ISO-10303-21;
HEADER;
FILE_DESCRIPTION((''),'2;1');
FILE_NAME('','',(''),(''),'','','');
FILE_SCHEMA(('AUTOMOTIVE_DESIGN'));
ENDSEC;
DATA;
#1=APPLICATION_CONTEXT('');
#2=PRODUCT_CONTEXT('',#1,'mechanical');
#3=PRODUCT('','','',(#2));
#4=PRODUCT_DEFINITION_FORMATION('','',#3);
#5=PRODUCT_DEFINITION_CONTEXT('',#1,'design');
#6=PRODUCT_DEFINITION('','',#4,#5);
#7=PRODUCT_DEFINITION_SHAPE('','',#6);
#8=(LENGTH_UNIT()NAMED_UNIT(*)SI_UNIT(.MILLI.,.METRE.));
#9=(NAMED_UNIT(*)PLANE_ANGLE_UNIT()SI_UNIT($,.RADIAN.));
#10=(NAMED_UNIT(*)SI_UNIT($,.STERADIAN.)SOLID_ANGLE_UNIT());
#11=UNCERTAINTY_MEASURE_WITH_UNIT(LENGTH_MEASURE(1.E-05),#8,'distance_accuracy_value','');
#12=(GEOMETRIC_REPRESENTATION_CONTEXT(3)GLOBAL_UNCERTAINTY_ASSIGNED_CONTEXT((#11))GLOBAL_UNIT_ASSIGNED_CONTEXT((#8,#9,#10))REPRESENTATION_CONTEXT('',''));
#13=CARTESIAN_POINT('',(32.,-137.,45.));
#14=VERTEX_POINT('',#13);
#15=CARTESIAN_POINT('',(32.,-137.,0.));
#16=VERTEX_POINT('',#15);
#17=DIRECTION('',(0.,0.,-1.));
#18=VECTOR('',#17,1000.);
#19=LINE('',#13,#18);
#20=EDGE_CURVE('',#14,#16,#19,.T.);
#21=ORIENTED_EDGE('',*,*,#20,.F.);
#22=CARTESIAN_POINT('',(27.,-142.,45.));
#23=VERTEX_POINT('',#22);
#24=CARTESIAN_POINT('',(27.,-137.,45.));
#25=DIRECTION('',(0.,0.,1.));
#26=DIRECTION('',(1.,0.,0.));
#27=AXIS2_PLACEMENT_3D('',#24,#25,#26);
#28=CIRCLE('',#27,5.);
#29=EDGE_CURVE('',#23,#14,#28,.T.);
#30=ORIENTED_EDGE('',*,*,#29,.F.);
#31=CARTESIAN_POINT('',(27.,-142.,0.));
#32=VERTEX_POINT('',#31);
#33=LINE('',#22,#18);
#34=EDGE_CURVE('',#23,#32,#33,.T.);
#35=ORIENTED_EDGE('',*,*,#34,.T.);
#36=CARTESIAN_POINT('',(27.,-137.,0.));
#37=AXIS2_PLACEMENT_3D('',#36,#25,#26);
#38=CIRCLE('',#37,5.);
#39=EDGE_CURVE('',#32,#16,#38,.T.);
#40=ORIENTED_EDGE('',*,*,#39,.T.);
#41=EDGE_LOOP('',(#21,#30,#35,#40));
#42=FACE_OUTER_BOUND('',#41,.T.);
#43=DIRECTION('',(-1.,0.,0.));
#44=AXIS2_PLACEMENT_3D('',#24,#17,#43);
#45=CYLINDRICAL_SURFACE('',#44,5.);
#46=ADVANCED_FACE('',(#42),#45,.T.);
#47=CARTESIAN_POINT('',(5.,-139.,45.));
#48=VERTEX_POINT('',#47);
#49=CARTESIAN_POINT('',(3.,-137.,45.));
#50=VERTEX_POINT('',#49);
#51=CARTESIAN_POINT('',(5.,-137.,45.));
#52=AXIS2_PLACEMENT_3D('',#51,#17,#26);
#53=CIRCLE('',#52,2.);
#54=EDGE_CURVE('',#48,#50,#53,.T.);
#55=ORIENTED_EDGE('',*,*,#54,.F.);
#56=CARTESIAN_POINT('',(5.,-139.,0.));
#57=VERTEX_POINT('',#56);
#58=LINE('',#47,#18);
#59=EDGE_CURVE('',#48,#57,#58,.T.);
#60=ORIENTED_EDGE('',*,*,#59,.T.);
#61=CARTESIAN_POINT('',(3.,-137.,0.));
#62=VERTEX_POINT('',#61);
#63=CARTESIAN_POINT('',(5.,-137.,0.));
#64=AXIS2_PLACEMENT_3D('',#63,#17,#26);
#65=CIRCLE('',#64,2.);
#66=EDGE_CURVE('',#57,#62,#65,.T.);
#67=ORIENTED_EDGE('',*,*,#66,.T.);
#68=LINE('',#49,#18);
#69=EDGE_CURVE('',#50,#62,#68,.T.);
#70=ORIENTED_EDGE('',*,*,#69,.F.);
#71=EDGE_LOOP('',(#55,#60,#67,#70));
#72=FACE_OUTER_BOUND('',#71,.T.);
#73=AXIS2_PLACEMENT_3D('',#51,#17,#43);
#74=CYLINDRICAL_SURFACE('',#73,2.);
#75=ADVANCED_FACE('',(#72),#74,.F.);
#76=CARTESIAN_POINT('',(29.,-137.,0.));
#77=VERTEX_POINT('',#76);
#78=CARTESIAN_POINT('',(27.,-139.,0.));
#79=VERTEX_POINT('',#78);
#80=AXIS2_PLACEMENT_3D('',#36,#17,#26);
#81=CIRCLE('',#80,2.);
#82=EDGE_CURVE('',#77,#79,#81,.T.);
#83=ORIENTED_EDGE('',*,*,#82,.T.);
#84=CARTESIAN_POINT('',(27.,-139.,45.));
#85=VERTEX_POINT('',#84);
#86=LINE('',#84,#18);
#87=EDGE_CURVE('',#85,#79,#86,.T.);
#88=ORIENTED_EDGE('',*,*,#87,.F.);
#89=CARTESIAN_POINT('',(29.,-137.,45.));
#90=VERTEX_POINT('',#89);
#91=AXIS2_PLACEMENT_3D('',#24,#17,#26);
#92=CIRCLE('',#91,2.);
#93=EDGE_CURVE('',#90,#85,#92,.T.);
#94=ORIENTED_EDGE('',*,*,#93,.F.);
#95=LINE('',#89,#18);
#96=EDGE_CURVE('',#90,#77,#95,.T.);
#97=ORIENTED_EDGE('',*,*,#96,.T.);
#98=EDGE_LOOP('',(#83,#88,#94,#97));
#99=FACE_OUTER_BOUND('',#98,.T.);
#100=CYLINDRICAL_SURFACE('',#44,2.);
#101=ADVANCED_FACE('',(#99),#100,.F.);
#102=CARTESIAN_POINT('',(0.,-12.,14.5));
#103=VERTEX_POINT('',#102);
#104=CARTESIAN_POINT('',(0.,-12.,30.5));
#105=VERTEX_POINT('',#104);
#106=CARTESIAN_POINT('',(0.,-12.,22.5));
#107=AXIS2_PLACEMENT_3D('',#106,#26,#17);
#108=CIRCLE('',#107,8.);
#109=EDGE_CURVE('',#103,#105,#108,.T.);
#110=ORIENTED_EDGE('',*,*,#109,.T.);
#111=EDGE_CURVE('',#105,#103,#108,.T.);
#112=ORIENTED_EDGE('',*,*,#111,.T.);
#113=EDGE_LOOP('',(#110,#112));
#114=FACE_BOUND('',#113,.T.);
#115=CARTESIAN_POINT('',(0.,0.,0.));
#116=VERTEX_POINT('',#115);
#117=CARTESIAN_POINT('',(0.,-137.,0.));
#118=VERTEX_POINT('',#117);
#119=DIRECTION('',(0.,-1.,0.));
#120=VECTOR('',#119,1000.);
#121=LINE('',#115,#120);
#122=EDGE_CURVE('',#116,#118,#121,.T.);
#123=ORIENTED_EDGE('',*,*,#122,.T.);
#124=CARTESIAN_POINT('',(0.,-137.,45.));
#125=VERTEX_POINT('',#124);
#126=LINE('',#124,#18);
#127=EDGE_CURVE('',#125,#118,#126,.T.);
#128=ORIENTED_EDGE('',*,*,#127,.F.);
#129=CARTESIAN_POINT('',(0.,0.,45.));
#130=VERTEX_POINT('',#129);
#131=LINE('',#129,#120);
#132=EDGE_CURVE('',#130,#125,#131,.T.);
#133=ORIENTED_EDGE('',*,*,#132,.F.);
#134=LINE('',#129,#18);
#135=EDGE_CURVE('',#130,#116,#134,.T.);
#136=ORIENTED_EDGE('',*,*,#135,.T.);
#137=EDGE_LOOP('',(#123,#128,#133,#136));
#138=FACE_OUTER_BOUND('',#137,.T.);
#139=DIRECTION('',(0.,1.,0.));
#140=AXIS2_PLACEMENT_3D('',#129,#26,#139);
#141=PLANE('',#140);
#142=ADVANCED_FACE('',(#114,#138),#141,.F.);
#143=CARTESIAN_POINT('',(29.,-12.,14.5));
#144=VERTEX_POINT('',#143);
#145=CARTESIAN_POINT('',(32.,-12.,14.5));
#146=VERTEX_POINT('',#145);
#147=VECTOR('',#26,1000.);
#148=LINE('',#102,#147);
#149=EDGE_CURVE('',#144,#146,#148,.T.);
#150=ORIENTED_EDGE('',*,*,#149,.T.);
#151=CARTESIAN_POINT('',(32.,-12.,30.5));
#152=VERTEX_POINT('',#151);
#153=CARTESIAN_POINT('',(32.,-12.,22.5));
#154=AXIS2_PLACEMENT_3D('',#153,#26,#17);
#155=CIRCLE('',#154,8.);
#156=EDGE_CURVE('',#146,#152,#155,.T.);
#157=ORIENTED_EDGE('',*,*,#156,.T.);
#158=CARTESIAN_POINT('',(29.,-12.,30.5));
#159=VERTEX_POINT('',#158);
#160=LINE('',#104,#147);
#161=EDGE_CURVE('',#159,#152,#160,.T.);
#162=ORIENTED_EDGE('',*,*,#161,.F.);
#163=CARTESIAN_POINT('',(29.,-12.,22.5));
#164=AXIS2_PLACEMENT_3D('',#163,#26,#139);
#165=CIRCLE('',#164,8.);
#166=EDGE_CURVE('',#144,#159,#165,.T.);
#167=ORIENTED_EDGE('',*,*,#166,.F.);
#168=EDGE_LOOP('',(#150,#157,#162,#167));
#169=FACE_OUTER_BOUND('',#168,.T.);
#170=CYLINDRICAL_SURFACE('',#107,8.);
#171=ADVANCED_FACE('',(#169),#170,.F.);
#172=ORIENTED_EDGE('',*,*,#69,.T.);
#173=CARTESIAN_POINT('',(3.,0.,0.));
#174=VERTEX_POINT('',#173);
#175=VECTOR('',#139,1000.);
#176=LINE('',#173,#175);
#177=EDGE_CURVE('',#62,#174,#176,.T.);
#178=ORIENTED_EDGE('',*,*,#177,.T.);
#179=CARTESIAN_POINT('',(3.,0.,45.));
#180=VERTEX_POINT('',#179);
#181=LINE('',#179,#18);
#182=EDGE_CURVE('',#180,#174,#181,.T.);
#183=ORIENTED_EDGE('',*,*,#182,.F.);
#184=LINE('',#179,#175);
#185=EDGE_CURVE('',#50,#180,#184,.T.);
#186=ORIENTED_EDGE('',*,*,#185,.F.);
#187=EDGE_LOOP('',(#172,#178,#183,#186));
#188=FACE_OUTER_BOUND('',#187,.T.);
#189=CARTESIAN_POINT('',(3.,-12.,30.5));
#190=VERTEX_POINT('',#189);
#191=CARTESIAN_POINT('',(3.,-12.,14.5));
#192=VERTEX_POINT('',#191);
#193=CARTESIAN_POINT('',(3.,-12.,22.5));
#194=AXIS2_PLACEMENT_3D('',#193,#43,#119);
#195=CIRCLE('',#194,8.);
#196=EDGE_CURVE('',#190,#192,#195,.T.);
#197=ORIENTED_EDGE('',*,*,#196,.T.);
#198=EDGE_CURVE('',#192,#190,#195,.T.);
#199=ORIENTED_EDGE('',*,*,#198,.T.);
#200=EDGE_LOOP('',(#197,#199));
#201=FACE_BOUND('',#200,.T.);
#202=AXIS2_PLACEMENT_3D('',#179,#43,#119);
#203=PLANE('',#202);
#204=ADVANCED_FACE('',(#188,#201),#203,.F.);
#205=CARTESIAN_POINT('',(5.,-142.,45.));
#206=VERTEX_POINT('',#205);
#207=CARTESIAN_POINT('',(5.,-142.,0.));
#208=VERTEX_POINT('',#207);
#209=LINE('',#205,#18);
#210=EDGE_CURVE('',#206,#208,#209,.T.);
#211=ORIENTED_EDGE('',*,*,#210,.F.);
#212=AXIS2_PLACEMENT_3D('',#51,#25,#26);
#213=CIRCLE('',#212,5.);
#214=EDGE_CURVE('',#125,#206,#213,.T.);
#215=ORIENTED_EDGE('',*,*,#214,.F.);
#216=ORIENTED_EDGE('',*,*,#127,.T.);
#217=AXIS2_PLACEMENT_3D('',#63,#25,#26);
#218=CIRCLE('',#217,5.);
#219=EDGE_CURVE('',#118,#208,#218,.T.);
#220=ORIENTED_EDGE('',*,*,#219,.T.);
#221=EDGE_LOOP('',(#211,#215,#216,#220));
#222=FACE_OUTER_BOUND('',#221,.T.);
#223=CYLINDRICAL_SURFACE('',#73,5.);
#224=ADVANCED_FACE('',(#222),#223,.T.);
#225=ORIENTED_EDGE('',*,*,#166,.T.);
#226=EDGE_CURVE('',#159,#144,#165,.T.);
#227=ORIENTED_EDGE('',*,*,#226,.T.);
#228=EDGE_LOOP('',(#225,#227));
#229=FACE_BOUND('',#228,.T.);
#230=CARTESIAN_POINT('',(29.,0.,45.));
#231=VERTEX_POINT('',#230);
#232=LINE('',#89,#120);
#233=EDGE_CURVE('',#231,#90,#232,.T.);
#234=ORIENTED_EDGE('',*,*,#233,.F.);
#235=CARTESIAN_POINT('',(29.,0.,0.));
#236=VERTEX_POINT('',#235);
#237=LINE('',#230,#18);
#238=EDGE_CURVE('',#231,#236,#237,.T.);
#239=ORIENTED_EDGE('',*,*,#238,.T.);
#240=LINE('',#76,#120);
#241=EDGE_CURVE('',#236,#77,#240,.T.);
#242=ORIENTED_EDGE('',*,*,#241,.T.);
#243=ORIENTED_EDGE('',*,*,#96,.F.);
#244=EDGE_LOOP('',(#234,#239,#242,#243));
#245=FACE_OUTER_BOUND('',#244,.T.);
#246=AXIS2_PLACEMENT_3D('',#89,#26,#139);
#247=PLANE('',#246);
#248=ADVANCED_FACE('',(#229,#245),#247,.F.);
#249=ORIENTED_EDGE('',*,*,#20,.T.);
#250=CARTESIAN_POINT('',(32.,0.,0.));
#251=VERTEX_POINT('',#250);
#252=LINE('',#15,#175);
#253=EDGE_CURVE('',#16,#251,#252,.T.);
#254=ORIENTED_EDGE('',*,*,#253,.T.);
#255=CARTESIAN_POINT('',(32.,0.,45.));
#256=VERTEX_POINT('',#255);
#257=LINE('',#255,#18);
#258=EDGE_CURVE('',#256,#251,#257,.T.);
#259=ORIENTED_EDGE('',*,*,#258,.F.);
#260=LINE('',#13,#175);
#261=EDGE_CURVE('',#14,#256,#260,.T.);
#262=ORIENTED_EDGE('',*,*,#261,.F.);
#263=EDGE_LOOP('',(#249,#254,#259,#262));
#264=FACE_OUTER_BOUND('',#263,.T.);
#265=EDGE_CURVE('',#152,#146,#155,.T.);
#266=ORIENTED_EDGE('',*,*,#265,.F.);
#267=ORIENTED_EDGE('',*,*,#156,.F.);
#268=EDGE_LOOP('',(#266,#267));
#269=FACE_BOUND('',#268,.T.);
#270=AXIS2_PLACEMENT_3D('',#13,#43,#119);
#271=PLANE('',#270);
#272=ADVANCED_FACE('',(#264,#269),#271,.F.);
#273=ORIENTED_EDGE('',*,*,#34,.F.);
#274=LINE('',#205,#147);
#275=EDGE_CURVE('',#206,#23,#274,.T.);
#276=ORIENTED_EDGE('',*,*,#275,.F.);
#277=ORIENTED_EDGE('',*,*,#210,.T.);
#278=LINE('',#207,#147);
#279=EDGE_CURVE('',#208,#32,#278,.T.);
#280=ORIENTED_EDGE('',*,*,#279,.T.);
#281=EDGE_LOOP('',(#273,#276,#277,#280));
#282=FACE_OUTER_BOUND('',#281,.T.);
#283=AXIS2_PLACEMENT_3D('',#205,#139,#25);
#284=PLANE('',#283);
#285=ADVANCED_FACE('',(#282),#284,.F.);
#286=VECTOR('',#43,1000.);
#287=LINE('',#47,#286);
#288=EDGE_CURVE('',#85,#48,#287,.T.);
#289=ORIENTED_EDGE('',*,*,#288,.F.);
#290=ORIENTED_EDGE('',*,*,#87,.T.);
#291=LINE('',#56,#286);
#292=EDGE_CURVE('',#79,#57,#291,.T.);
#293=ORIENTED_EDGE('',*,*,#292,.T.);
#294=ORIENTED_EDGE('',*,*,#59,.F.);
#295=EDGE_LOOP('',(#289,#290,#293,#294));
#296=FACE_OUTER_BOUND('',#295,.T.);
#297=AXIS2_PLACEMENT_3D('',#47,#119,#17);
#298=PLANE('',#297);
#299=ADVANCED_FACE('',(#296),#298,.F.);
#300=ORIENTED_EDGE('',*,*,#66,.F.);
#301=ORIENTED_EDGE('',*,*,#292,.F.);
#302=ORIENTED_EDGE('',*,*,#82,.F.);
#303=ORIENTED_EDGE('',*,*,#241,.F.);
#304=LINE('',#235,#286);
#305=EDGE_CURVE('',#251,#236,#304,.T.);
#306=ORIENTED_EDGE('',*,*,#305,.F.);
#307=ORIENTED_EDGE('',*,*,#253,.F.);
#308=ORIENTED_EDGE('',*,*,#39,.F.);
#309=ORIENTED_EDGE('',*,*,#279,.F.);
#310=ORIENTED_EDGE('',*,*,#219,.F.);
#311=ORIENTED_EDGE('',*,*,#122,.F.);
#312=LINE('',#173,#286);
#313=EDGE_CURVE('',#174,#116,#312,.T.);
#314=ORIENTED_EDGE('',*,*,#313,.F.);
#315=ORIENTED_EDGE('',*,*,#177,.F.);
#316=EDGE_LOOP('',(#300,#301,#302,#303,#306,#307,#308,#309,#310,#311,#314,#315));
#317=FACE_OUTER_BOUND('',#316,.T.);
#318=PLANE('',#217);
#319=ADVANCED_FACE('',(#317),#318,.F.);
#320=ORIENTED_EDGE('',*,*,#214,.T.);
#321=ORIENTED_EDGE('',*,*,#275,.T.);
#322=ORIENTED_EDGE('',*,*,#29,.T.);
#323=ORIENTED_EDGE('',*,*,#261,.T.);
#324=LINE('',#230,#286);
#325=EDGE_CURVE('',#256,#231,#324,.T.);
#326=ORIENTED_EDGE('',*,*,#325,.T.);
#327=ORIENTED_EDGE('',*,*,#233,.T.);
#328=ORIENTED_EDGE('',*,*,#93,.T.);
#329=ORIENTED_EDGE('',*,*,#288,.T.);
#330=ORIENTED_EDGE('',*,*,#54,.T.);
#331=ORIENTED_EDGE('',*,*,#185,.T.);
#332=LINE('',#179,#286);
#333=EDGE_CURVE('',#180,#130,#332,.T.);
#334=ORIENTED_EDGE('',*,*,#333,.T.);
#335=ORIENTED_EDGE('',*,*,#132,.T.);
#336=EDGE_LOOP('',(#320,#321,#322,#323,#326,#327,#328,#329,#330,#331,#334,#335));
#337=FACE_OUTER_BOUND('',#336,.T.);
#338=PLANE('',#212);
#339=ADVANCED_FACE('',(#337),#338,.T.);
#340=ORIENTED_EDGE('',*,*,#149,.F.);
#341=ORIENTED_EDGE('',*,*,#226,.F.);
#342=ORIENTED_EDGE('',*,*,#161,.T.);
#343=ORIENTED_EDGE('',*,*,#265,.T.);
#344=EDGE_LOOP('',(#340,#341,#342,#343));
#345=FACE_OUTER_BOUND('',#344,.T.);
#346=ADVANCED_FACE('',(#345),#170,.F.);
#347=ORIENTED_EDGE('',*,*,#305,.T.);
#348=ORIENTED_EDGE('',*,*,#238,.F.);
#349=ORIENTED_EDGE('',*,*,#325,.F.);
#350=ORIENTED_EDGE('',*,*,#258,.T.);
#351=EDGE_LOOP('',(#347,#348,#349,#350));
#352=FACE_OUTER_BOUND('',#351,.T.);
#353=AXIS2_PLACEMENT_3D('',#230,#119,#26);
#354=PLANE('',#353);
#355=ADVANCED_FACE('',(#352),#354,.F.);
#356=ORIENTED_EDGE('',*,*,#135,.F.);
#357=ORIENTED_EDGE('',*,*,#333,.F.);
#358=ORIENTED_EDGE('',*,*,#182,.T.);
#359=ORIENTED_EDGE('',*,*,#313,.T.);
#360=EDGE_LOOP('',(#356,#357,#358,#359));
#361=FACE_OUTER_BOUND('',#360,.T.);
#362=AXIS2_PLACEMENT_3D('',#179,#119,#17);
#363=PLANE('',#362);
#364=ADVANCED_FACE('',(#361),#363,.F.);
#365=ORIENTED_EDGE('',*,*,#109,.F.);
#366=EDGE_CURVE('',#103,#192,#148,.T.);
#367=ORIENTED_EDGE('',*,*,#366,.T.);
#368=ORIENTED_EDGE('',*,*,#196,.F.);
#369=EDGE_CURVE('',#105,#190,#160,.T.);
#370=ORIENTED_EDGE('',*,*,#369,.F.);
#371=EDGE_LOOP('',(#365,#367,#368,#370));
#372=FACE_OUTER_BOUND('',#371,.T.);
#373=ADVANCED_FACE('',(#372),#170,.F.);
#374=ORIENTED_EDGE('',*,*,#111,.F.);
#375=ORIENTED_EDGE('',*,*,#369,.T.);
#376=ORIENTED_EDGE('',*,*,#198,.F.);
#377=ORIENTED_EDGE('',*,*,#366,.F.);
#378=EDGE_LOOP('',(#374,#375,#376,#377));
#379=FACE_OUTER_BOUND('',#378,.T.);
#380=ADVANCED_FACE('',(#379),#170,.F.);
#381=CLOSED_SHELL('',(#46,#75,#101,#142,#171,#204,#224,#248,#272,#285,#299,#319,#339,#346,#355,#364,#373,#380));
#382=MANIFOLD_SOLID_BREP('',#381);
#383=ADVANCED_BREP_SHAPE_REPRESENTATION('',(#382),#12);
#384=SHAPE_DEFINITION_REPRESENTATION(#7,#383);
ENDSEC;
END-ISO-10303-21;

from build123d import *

# Parameters (mm, degrees)
BOSS_EXTRUDE1_DEPTH = 45
SKETCH2_R           = 8
CUT_EXTRUDE1_DEPTH  = 153.358130732


with BuildPart() as part:
    # Sketch1 → Boss-Extrude1 (new body)
    with BuildSketch(Plane.XY):
        with BuildLine():
            Line((0, 0), (0, -137))
            ThreePointArc((0, -137), (1.464466094, -140.535533906), (5, -142))
            Line((5, -142), (27, -142))
            ThreePointArc((27, -142), (30.535533906, -140.535533906), (32, -137))
            Line((32, -137), (32, 0))
            Line((32, 0), (29, 0))
            Line((29, 0), (29, -137))
            ThreePointArc((29, -137), (28.414213562, -138.414213562), (27, -139))
            Line((27, -139), (5, -139))
            ThreePointArc((5, -139), (3.585786438, -138.414213562), (3, -137))
            Line((3, -137), (3, 0))
            Line((3, 0), (0, 0))
        make_face()
    extrude(amount=BOSS_EXTRUDE1_DEPTH)

    # Sketch2 → Cut-Extrude1 (cut, through all)
    with BuildSketch(Plane(origin=(32, 0, 0), x_dir=(0, 0, -1), z_dir=(1, 0, 0))):
        with Locations((-22.5, -12)):
            Circle(SKETCH2_R)
    extrude(amount=-CUT_EXTRUDE1_DEPTH, mode=Mode.SUBTRACT)


solid = part.part
